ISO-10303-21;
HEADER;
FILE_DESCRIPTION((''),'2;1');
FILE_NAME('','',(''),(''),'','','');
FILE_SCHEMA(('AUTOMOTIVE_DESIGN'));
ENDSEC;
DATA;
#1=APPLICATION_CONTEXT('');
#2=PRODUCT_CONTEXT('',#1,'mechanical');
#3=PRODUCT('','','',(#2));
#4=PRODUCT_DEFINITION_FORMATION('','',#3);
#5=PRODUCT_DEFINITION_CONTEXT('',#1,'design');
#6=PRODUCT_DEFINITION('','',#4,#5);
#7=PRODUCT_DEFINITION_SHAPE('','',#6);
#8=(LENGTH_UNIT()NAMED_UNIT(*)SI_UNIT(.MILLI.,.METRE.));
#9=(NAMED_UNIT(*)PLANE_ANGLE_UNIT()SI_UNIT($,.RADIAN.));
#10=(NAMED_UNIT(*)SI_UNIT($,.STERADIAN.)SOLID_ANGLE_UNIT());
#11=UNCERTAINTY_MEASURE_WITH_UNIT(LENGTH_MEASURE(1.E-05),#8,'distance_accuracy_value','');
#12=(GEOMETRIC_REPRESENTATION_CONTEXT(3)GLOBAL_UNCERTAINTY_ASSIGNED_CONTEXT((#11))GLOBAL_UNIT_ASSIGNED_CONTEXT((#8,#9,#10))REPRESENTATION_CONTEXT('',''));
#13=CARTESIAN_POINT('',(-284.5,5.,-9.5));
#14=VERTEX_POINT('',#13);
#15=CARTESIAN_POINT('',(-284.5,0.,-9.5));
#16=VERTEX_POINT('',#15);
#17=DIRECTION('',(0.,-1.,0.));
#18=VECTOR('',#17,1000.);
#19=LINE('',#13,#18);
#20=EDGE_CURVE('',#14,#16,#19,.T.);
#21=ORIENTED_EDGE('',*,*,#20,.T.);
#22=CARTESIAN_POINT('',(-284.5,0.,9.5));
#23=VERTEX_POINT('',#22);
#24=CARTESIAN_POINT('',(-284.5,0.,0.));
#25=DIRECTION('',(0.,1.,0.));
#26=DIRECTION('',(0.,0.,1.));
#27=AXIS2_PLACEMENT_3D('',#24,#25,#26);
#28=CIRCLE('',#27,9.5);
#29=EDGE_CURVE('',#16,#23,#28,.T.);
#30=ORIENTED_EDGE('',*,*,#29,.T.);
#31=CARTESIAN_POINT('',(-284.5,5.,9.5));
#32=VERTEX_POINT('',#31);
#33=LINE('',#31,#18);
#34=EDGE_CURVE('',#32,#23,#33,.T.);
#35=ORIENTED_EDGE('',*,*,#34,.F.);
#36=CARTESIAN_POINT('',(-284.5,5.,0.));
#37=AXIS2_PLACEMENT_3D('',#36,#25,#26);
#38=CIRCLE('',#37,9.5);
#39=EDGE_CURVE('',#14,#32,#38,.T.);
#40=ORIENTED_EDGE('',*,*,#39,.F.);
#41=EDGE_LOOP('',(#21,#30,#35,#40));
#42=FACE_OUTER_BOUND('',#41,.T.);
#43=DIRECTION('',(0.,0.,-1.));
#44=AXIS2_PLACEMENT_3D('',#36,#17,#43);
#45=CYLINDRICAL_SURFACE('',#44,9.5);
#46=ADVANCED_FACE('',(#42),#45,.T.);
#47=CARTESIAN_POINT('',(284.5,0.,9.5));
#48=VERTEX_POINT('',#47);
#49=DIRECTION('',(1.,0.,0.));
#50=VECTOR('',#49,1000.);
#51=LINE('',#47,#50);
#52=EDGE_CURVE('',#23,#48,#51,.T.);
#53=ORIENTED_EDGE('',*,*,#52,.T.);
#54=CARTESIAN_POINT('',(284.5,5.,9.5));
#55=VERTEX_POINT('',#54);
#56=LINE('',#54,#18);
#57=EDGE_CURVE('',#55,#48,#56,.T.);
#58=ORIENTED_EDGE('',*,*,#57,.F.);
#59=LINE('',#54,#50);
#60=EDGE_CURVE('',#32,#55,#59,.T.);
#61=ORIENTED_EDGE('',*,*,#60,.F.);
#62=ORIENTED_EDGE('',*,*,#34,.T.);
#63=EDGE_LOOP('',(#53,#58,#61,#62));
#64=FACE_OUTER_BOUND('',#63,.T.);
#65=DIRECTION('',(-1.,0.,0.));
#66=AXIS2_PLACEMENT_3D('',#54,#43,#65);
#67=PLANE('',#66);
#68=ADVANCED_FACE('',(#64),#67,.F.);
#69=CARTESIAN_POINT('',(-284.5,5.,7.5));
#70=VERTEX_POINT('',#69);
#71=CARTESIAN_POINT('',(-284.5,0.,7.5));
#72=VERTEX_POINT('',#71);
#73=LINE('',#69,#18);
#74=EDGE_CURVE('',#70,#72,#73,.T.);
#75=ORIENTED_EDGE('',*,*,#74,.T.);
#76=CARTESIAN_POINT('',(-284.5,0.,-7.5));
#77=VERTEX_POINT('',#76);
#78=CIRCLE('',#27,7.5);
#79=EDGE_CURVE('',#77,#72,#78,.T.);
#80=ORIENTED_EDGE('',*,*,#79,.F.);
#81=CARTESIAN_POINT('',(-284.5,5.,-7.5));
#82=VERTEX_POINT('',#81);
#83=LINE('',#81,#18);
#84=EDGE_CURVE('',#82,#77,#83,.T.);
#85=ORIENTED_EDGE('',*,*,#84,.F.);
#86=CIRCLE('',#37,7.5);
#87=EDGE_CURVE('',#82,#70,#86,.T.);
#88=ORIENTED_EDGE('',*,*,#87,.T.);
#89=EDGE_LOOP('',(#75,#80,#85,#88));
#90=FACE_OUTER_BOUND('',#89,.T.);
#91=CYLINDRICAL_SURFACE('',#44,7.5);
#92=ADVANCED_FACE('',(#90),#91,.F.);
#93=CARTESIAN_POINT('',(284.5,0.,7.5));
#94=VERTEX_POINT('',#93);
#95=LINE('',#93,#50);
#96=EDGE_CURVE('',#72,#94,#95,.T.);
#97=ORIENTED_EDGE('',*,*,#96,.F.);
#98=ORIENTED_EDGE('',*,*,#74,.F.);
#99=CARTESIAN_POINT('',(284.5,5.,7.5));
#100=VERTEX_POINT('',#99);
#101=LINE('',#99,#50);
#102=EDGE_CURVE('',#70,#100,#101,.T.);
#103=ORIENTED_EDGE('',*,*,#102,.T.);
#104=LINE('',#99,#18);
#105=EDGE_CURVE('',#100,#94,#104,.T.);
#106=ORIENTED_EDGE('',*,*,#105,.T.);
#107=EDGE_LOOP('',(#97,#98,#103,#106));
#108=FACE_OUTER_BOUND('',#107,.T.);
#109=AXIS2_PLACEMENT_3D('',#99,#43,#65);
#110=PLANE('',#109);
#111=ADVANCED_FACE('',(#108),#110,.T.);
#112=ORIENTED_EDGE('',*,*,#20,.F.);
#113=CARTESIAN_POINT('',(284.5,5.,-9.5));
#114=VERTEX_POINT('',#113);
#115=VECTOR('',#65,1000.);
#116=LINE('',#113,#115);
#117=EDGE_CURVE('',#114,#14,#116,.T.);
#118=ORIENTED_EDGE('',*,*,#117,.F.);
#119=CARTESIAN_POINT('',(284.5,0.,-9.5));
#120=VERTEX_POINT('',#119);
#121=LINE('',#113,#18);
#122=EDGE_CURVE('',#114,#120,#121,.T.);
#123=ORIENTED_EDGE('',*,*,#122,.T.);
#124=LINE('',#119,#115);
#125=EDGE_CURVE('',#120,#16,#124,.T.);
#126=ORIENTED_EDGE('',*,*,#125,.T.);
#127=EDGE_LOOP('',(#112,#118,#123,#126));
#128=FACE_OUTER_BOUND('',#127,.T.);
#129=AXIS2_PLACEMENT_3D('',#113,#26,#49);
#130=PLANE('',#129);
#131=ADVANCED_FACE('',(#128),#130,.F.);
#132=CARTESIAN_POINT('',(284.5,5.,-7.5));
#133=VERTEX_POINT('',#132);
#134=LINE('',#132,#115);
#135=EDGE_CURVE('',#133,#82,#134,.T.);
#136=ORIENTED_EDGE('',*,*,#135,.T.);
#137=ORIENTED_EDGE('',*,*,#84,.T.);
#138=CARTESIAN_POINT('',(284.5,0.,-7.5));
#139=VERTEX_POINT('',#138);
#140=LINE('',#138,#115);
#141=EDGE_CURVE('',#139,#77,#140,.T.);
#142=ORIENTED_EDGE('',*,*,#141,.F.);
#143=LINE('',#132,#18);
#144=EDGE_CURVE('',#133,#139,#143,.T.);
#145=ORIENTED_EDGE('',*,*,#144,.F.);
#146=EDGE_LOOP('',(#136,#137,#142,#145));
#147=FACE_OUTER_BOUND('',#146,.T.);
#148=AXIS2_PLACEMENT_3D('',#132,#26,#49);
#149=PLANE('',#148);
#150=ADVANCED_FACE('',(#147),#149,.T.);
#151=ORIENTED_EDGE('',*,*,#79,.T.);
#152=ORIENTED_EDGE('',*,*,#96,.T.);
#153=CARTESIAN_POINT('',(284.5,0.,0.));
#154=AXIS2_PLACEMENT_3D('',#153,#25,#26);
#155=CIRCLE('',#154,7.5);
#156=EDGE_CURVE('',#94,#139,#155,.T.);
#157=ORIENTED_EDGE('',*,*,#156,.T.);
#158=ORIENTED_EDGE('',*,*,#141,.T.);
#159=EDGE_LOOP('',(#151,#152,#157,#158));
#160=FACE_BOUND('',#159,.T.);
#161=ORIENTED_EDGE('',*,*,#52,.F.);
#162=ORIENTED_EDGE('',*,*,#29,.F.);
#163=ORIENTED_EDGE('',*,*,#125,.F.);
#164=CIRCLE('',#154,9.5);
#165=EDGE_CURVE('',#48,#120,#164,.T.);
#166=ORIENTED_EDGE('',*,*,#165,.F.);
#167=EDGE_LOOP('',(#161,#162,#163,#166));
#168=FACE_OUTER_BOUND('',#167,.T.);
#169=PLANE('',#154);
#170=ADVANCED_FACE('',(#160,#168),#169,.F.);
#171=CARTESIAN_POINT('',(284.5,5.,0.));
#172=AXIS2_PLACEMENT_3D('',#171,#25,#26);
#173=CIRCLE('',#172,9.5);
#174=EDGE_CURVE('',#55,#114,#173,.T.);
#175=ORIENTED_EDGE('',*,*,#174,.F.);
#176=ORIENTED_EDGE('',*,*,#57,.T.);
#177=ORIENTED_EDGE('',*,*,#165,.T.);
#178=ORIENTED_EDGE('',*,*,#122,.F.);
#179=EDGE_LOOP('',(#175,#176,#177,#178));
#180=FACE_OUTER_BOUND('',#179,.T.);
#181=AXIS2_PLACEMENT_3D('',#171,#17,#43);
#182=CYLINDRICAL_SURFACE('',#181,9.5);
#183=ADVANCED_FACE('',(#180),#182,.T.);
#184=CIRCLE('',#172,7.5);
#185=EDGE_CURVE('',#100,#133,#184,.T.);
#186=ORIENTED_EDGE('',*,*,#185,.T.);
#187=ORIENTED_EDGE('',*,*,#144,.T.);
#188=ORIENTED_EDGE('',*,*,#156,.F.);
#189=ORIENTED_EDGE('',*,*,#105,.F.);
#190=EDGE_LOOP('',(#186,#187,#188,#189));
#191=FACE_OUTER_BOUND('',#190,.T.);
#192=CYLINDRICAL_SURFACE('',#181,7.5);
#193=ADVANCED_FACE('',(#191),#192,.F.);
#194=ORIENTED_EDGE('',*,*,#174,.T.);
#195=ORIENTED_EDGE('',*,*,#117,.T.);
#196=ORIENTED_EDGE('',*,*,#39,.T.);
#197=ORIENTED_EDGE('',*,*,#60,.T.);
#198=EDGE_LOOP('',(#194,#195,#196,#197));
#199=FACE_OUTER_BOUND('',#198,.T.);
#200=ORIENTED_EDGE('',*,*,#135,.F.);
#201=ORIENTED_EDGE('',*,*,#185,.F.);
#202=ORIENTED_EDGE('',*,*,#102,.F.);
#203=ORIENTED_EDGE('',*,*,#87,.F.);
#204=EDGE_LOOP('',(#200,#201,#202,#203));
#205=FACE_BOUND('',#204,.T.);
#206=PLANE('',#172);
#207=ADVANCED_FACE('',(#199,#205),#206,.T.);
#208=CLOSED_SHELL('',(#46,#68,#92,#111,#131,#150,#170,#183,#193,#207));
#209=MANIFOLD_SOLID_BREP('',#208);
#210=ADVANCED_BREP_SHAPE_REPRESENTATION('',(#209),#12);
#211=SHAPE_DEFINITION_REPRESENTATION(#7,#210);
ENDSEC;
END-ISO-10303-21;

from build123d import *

# Parameters (mm, degrees)
BOSS_EXTRUDE1_DEPTH = 5


with BuildPart() as part:
    # Sketch1 → Boss-Extrude1 (new body)
    with BuildSketch(Plane(origin=(0, 0, 0), x_dir=(1, 0, 0), z_dir=(0, 1, 0))):
        with BuildLine():
            Line((284.5, -9.5), (-284.5, -9.5))
            ThreePointArc((-284.5, -9.5), (-294, 0), (-284.5, 9.5))
            Line((-284.5, 9.5), (284.5, 9.5))
            ThreePointArc((284.5, 9.5), (294, 0), (284.5, -9.5))
        make_face()
        with BuildLine():
            Line((284.5, -7.5), (-284.5, -7.5))
            ThreePointArc((-284.5, -7.5), (-292, 0), (-284.5, 7.5))
            Line((-284.5, 7.5), (284.5, 7.5))
            ThreePointArc((284.5, 7.5), (292, 0), (284.5, -7.5))
        make_face(mode=Mode.SUBTRACT)
    extrude(amount=BOSS_EXTRUDE1_DEPTH)


solid = part.part
